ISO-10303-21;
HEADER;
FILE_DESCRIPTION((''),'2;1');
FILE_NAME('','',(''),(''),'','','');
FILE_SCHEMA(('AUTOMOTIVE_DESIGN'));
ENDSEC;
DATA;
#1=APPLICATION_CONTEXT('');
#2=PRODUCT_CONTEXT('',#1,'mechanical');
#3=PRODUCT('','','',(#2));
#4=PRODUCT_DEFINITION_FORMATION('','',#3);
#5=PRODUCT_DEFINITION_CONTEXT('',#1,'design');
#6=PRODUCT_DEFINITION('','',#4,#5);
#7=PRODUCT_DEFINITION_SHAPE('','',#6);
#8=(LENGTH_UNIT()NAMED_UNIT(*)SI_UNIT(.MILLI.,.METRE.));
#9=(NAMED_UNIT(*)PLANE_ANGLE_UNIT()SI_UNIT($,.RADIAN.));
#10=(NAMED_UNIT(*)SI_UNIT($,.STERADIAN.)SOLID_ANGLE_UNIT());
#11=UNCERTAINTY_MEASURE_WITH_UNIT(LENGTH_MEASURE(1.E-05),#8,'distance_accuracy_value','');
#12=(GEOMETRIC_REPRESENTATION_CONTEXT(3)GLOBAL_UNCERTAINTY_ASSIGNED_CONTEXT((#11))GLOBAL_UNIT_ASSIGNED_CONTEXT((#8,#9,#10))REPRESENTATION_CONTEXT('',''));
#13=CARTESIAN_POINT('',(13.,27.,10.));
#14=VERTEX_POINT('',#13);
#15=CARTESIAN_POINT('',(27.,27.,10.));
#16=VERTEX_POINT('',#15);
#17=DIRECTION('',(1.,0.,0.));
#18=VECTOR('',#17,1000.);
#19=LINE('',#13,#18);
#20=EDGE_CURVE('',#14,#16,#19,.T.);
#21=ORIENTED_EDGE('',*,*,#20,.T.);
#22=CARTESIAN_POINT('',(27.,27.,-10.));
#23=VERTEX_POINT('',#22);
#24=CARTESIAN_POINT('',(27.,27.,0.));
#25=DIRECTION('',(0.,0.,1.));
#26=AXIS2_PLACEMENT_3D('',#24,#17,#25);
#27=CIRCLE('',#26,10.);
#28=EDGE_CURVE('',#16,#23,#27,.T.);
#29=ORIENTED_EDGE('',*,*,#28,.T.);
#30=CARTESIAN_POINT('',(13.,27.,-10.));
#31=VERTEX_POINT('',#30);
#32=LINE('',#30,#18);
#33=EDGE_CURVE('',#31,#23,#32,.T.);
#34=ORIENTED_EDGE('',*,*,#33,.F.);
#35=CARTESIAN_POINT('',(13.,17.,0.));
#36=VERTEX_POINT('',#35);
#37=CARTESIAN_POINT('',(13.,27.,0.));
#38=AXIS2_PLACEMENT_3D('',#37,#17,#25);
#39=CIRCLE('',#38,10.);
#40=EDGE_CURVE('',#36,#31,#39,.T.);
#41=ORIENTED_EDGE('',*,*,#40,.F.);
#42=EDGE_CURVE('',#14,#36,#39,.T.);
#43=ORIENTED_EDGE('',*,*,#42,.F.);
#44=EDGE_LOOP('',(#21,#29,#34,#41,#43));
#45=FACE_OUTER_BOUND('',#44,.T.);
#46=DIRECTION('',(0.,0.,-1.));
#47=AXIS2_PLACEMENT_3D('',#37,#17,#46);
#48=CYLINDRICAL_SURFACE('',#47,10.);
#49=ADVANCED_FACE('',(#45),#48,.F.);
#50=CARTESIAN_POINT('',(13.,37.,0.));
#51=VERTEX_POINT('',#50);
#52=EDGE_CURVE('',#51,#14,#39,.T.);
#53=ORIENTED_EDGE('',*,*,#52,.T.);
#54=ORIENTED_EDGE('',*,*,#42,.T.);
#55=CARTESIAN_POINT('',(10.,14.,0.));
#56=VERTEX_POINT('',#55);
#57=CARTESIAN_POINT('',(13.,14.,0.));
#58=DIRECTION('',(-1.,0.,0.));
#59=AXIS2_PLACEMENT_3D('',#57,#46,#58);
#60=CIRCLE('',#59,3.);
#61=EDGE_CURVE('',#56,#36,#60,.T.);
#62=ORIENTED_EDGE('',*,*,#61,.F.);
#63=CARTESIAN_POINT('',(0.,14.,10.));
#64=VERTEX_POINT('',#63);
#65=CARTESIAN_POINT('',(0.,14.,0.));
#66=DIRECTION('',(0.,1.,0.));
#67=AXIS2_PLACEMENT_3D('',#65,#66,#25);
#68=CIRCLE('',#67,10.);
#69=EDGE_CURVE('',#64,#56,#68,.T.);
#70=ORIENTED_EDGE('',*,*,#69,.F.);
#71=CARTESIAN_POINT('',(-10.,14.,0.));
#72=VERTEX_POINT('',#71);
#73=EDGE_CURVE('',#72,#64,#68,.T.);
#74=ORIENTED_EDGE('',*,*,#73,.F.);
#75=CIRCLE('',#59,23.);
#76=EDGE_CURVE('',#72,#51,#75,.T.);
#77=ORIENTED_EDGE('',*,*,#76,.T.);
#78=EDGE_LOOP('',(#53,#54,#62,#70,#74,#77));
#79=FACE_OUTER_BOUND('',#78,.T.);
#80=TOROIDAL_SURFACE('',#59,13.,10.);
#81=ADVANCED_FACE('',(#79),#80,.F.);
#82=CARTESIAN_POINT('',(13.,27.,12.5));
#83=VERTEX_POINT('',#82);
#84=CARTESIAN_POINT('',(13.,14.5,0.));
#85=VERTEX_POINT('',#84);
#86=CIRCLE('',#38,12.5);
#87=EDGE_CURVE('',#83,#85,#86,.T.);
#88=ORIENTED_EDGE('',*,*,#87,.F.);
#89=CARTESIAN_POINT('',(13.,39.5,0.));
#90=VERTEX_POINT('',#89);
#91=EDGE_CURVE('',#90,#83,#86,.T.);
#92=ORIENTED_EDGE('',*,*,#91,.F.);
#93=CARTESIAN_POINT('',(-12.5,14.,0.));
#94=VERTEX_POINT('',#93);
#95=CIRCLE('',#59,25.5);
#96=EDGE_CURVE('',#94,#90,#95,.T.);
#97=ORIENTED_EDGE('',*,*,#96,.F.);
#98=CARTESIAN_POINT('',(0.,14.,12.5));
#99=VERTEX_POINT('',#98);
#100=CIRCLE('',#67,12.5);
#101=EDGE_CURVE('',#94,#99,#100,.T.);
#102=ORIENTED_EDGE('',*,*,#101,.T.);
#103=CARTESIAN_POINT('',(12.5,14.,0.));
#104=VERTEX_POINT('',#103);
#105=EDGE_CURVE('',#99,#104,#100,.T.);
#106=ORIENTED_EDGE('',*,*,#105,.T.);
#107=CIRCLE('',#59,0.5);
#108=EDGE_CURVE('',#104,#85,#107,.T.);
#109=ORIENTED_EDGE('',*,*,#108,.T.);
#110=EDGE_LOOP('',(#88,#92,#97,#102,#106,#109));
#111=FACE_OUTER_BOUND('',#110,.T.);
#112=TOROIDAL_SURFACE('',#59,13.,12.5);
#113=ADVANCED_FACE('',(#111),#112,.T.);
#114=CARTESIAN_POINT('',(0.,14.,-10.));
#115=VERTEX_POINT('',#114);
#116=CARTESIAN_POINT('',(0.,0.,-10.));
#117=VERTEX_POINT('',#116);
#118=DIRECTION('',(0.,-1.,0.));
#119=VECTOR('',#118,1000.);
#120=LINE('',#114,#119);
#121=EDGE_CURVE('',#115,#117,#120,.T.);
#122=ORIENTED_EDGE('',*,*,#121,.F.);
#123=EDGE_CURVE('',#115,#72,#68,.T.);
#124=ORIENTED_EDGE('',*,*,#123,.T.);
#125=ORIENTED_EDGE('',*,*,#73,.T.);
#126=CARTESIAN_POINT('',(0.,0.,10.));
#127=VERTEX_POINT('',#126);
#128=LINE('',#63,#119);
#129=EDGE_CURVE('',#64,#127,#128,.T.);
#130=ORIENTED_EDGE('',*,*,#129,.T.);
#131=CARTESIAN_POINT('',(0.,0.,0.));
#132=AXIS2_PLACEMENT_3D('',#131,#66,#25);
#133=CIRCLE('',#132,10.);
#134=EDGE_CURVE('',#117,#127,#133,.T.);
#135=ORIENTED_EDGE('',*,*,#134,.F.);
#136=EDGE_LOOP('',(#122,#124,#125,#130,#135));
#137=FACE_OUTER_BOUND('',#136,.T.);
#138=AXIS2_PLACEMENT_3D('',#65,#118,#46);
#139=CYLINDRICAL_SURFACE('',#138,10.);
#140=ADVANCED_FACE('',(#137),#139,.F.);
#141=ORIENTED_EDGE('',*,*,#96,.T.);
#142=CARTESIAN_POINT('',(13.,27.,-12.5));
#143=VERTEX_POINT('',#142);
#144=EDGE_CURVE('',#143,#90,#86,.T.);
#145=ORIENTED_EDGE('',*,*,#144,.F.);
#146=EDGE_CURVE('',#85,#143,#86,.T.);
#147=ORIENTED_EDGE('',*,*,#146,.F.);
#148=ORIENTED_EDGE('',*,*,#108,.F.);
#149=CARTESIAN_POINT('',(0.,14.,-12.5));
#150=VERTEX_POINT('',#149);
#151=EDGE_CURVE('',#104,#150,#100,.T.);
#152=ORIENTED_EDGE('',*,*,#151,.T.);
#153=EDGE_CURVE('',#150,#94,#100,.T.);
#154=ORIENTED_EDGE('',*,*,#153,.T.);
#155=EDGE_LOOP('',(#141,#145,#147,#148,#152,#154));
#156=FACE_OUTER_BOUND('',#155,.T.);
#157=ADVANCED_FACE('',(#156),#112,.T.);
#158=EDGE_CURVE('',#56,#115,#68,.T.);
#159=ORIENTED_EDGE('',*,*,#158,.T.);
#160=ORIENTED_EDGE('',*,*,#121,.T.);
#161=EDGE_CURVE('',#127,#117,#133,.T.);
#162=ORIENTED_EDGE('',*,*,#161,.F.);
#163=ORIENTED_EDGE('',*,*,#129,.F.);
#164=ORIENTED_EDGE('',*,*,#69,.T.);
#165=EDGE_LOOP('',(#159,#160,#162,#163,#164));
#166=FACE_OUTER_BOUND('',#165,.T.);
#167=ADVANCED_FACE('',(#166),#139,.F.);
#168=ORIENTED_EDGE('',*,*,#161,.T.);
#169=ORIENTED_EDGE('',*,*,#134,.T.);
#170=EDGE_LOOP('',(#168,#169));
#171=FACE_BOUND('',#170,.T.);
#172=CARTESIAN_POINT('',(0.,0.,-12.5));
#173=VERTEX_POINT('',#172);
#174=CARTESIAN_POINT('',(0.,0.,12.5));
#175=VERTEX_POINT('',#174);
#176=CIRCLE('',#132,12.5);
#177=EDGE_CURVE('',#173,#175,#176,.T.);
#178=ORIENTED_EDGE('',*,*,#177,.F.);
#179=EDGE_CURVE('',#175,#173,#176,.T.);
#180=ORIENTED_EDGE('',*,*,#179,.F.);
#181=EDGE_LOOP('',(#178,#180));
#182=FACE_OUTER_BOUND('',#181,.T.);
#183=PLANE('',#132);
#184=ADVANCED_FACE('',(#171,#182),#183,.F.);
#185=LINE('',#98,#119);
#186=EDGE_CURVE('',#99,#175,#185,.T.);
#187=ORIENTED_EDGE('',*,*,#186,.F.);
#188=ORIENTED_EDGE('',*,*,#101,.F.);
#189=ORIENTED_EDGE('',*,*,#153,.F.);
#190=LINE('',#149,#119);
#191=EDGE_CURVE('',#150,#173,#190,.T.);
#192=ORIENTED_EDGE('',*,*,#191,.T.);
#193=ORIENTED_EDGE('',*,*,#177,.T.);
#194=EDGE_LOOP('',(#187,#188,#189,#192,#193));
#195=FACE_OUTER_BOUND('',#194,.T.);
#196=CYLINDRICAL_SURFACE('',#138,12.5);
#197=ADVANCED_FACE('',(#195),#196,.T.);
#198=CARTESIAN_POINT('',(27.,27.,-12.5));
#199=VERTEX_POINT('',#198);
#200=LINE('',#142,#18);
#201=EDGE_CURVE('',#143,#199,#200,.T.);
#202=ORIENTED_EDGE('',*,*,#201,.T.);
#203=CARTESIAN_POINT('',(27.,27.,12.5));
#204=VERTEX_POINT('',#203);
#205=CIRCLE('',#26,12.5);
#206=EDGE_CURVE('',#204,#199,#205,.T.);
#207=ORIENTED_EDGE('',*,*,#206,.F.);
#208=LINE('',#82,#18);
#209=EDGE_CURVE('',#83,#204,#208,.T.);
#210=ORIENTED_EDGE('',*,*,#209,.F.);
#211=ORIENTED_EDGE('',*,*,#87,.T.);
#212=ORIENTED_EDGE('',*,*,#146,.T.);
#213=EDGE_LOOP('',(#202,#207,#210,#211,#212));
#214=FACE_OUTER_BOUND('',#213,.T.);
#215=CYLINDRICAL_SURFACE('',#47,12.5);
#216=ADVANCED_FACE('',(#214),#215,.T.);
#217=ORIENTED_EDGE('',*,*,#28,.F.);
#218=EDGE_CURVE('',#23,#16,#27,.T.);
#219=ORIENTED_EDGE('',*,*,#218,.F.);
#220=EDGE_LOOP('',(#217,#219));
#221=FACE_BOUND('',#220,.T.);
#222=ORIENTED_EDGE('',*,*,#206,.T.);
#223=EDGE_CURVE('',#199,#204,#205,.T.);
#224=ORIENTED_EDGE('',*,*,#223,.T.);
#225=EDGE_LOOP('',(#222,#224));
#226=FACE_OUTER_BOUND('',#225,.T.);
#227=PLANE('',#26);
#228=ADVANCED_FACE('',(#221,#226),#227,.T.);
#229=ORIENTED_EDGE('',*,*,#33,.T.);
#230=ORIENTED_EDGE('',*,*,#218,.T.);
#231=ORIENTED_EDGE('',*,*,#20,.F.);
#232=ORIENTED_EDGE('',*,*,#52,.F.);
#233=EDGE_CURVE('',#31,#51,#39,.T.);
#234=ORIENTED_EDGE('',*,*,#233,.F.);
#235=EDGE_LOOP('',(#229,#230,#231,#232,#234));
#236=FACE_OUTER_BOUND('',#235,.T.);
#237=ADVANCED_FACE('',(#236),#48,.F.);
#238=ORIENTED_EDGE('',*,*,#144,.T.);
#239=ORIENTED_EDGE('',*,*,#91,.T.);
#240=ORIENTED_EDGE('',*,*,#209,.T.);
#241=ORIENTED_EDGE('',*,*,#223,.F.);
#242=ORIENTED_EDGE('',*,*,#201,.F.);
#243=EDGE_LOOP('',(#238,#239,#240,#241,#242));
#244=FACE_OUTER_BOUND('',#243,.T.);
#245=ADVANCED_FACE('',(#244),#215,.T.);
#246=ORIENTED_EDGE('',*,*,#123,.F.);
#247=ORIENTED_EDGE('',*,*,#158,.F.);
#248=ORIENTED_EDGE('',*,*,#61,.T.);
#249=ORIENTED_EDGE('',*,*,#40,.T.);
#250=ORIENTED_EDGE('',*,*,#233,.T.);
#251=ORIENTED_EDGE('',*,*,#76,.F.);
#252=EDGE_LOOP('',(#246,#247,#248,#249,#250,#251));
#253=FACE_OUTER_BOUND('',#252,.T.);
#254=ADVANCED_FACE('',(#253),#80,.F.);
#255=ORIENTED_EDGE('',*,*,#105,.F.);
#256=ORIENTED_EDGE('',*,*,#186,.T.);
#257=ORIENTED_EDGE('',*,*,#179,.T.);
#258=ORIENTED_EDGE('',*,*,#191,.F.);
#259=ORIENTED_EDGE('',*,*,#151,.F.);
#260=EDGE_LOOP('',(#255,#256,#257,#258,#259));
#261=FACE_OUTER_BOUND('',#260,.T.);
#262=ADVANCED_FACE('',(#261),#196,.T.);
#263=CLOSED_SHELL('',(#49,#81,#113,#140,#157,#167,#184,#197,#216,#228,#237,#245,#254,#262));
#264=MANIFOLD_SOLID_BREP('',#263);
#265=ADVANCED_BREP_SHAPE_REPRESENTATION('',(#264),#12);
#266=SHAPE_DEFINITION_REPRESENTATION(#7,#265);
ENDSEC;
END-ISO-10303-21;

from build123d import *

# Parameters (mm, degrees)
SKETCH_2_R   = 12.5
SKETCH_2_R_2 = 10


with BuildPart() as part:
    # 扫描1: sweep along a path in 草图1
    with BuildLine(Plane.XY) as sweep_1_path:
        Line((0, 0), (0, 14))
        ThreePointArc((0, 14), (3.807611845, 23.192388155), (13, 27))
        Line((13, 27), (27, 27))
    # 草图2 → 扫描1 (sweep)
    with BuildSketch(Plane(origin=(0, 0, 0), x_dir=(1, 0, 0), z_dir=(0, 1, 0))):
        Circle(SKETCH_2_R)
        Circle(SKETCH_2_R_2, mode=Mode.SUBTRACT)
    sweep(path=sweep_1_path.line)


solid = part.part
